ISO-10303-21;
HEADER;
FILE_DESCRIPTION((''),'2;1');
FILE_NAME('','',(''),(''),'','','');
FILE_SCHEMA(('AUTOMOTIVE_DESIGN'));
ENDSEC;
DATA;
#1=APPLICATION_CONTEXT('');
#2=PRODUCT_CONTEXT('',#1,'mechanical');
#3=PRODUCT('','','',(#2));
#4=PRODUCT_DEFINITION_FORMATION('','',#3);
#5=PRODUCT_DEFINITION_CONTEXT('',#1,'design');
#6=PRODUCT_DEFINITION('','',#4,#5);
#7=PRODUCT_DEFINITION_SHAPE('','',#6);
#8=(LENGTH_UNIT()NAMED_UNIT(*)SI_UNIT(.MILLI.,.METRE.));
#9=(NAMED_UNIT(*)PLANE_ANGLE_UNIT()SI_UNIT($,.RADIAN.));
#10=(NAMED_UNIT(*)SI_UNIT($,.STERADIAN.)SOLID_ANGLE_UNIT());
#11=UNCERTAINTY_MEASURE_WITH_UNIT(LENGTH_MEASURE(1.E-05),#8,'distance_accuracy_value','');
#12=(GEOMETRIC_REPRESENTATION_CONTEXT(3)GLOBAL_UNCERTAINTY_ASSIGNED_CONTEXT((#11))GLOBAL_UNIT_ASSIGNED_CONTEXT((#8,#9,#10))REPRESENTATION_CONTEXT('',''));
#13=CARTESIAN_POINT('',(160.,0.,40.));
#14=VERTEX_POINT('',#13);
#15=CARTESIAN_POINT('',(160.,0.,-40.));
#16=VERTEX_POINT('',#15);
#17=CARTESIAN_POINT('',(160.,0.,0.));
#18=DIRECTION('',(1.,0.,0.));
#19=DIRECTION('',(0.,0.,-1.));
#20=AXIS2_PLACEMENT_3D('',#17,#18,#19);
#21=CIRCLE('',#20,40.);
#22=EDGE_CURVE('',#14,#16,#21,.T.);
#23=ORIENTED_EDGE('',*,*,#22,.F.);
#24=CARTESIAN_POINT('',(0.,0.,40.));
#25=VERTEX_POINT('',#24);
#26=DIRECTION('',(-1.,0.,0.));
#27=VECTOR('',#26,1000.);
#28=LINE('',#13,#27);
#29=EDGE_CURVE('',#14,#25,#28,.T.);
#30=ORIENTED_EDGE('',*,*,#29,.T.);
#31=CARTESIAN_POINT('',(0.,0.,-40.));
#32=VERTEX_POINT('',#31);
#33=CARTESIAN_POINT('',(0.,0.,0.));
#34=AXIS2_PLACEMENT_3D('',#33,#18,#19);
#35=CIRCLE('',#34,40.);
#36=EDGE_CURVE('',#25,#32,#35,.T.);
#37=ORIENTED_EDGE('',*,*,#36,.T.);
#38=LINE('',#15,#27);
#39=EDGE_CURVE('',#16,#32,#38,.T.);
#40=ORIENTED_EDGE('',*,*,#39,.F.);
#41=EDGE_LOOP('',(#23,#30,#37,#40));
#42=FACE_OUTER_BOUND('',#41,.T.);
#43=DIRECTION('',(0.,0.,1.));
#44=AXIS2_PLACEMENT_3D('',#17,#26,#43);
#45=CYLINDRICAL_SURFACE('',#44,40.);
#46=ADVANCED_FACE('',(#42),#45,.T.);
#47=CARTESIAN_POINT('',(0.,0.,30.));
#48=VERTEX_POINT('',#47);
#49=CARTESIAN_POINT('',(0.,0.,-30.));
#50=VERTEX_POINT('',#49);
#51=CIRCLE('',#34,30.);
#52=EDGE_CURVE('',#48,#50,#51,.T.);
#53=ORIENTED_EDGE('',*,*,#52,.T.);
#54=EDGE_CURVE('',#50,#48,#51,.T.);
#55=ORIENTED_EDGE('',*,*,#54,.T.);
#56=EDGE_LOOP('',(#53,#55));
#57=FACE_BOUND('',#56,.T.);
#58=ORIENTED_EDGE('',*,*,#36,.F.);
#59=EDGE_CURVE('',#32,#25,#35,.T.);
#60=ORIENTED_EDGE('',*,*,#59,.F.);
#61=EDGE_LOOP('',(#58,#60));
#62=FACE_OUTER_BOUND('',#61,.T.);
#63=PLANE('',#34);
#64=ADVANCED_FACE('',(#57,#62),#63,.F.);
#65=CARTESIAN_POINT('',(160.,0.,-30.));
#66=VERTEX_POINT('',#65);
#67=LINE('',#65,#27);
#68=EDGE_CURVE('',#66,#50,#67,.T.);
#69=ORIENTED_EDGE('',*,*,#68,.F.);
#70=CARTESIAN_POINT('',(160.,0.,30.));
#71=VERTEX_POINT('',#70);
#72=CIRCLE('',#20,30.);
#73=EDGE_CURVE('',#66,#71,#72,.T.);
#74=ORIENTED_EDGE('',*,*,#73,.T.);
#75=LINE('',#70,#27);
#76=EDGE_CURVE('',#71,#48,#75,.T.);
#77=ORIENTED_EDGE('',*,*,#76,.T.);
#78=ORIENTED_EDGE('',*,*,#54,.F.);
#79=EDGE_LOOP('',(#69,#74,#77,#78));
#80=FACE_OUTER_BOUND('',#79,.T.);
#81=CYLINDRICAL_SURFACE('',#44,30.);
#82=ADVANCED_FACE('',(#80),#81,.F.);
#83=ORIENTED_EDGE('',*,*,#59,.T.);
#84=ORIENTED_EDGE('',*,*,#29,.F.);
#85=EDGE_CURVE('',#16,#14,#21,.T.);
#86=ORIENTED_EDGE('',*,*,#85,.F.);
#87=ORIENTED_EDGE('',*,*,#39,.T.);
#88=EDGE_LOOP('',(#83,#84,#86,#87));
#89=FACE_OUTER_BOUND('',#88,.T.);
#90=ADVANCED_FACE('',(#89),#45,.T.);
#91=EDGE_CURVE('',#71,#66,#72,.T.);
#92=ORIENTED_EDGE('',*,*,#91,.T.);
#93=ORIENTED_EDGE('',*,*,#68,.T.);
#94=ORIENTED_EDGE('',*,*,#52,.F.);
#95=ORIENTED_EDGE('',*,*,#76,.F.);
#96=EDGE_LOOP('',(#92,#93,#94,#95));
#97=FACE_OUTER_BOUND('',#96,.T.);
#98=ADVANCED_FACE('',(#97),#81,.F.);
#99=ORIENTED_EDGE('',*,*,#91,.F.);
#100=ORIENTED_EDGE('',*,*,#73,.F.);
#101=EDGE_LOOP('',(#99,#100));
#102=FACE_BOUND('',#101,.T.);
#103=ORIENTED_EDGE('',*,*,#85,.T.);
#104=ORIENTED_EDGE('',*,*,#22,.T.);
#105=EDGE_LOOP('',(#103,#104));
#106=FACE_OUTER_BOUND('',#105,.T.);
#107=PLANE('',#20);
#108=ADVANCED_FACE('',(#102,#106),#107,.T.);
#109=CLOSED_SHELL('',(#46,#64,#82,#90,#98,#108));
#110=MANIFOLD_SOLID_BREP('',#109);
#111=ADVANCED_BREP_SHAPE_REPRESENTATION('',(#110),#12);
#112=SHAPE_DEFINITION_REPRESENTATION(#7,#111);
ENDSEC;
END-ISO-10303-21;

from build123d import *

# Parameters (mm, degrees)
SKETCH1_R           = 40
SKETCH1_R_2         = 30
BOSS_EXTRUDE1_DEPTH = 160


with BuildPart() as part:
    # Sketch1 → Boss-Extrude1 (new body)
    with BuildSketch(Plane(origin=(0, 0, 0), x_dir=(0, 0, -1), z_dir=(1, 0, 0))):
        Circle(SKETCH1_R)
        Circle(SKETCH1_R_2, mode=Mode.SUBTRACT)
    extrude(amount=BOSS_EXTRUDE1_DEPTH)


solid = part.part
